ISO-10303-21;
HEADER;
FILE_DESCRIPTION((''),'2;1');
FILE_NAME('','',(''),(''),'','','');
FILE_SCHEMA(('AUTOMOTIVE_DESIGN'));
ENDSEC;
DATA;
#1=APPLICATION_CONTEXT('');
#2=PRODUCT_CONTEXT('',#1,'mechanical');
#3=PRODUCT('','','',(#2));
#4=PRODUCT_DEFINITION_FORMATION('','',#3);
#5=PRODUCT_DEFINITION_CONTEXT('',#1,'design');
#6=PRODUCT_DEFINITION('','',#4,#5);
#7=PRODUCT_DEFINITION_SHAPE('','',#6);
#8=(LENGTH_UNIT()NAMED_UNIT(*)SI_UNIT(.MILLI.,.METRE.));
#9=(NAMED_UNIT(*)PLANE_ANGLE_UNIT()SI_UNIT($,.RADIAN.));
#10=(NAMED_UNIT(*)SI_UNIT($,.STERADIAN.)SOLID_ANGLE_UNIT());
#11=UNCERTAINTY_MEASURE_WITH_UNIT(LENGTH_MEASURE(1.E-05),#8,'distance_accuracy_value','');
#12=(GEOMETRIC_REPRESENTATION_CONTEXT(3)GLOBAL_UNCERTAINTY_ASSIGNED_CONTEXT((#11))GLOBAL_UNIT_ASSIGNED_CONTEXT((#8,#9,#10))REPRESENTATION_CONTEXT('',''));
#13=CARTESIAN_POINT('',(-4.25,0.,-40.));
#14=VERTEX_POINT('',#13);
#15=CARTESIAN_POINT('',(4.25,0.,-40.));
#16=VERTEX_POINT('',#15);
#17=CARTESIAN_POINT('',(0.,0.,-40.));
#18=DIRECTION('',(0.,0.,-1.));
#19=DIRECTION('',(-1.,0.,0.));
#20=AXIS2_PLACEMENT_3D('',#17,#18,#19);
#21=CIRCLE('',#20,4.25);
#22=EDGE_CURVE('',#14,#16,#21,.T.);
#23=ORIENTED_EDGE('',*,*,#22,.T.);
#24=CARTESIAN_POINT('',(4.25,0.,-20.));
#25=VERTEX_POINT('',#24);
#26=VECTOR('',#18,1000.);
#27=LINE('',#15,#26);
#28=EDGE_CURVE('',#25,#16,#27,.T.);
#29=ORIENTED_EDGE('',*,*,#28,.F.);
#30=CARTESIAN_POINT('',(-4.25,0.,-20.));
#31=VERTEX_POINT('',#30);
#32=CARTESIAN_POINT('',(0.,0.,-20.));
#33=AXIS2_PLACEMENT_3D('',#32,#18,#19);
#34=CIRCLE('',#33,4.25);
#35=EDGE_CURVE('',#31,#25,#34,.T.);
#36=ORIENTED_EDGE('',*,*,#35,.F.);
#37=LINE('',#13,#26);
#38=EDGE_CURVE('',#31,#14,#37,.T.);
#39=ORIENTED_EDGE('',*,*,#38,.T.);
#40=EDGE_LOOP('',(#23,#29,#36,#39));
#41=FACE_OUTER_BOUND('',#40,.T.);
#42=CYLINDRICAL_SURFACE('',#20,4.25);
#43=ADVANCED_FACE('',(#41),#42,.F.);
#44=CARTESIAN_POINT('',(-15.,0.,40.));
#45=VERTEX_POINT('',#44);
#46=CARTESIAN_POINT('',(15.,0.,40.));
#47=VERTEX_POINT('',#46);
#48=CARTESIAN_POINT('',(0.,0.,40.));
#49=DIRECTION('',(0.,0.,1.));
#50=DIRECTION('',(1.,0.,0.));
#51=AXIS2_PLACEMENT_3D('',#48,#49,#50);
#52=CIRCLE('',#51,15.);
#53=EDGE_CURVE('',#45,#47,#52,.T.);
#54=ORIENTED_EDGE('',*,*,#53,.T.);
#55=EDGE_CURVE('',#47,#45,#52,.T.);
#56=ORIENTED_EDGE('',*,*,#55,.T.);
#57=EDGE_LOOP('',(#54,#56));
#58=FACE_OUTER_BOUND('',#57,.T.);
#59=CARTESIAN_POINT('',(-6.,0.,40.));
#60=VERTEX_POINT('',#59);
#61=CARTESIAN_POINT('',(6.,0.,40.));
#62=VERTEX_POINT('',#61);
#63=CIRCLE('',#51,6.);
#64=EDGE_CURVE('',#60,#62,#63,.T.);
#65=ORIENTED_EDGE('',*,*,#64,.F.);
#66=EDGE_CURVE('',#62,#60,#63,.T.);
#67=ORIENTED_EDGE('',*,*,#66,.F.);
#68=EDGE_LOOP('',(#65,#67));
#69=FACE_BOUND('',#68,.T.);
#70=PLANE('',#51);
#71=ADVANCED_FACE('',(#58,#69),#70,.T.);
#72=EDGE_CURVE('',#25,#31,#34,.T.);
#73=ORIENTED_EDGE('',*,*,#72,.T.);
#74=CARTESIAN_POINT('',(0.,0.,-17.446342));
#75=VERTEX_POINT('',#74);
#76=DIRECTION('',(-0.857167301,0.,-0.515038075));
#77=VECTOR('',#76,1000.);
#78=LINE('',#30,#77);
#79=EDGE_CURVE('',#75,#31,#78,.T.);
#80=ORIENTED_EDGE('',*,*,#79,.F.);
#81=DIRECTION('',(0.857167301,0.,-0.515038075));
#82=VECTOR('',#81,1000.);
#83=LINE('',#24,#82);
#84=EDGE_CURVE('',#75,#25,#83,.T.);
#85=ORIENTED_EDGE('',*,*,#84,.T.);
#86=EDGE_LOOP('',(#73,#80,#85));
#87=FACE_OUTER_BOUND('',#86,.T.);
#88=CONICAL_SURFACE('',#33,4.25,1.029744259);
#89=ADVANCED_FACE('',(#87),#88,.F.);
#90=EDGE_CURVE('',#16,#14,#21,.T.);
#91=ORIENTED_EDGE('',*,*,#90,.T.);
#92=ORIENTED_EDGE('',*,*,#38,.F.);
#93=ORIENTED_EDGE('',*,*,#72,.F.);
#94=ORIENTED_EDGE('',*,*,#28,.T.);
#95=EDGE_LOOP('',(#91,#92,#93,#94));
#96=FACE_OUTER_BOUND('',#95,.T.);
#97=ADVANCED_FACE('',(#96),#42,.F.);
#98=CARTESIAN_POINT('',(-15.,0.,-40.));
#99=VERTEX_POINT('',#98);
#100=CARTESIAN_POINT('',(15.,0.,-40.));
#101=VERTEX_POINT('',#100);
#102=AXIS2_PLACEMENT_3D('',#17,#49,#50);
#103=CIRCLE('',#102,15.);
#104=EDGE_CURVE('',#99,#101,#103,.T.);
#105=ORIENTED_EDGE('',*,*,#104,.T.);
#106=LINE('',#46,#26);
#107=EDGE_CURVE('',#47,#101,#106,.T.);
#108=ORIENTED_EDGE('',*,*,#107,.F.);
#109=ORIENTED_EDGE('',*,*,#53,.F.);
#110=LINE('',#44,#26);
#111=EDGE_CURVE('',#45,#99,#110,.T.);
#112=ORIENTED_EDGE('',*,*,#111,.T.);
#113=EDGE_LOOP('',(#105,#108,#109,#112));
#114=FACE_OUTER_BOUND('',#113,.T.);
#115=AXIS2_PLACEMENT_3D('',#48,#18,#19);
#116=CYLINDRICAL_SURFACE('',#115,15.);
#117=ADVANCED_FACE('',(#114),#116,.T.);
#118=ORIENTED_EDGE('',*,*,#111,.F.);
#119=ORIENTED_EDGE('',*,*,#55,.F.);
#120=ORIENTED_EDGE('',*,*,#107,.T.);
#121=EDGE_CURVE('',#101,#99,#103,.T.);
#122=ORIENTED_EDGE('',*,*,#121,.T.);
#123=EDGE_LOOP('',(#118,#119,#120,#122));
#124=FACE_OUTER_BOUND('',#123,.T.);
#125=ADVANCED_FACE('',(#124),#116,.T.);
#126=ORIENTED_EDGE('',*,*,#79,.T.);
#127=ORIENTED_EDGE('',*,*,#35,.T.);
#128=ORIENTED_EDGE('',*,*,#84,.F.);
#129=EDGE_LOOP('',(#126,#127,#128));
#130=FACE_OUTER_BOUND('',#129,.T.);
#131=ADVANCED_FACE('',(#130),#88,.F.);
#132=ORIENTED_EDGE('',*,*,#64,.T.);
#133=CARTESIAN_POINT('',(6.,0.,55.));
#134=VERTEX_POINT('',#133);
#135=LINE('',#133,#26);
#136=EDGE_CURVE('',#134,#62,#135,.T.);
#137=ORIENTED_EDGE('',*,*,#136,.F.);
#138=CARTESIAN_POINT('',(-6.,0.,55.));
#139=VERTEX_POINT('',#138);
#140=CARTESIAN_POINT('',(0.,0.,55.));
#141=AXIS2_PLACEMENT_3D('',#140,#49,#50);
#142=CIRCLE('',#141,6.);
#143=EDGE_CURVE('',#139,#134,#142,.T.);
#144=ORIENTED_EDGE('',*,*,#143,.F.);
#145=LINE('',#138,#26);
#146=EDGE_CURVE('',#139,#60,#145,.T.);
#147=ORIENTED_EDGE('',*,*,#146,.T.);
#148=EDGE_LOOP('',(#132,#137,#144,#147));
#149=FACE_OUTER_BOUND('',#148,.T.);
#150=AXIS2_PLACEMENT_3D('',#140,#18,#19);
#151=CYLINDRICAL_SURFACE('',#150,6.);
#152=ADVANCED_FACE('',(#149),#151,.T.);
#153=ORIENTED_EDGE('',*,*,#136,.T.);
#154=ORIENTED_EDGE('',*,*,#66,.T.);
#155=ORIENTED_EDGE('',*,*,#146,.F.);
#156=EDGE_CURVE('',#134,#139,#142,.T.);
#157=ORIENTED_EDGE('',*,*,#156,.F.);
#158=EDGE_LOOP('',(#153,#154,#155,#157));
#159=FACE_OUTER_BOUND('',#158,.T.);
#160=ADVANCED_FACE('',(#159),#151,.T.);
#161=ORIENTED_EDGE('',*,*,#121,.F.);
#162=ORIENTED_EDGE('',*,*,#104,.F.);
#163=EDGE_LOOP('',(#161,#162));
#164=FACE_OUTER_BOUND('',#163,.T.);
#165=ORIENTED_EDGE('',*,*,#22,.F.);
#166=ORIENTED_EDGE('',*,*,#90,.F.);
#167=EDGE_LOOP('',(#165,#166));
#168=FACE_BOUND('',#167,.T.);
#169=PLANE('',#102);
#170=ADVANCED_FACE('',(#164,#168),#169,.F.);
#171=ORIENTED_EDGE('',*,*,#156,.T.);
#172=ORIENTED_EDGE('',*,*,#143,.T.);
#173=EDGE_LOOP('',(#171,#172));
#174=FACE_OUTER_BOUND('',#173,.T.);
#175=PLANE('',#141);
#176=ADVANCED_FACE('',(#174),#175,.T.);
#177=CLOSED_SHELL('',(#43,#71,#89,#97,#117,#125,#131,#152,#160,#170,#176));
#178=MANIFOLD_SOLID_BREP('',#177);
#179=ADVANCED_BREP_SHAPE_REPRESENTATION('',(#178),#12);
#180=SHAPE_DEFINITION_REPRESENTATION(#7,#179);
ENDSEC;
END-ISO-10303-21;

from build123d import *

# Parameters (mm, degrees)
SKETCH_1_R              = 15
EXTRUDE_1_DEPTH         = 40
HOLE_WIZARD_M10_1_D     = 8.5
HOLE_WIZARD_M10_1_DEPTH = 20
HOLE_WIZARD_M10_1_TIP   = 2.553657631
SKETCH_4_R              = 6
EXTRUDE_2_DEPTH         = 15


with BuildPart() as part:
    # 草图1 → 凸台-拉伸1 (new, symmetric)
    with BuildSketch(Plane.XY):
        Circle(SKETCH_1_R)
    extrude(amount=EXTRUDE_1_DEPTH, both=True)

    # M10 螺纹孔1
    with Locations(Plane(origin=(0, 0, -40), x_dir=(-1, 0, 0), z_dir=(0, 0, -1))):
        with Locations((0, 0)):
            Hole(HOLE_WIZARD_M10_1_D / 2, depth=HOLE_WIZARD_M10_1_DEPTH)
            with Locations((0, 0, -(HOLE_WIZARD_M10_1_DEPTH + HOLE_WIZARD_M10_1_TIP / 2))):  # 118° drill point
                Cone(0, HOLE_WIZARD_M10_1_D / 2, HOLE_WIZARD_M10_1_TIP, mode=Mode.SUBTRACT)

    # 草图4 → 凸台-拉伸2 (add)
    with BuildSketch(Plane.XY.offset(40)):
        Circle(SKETCH_4_R)
    extrude(amount=EXTRUDE_2_DEPTH)


solid = part.part
